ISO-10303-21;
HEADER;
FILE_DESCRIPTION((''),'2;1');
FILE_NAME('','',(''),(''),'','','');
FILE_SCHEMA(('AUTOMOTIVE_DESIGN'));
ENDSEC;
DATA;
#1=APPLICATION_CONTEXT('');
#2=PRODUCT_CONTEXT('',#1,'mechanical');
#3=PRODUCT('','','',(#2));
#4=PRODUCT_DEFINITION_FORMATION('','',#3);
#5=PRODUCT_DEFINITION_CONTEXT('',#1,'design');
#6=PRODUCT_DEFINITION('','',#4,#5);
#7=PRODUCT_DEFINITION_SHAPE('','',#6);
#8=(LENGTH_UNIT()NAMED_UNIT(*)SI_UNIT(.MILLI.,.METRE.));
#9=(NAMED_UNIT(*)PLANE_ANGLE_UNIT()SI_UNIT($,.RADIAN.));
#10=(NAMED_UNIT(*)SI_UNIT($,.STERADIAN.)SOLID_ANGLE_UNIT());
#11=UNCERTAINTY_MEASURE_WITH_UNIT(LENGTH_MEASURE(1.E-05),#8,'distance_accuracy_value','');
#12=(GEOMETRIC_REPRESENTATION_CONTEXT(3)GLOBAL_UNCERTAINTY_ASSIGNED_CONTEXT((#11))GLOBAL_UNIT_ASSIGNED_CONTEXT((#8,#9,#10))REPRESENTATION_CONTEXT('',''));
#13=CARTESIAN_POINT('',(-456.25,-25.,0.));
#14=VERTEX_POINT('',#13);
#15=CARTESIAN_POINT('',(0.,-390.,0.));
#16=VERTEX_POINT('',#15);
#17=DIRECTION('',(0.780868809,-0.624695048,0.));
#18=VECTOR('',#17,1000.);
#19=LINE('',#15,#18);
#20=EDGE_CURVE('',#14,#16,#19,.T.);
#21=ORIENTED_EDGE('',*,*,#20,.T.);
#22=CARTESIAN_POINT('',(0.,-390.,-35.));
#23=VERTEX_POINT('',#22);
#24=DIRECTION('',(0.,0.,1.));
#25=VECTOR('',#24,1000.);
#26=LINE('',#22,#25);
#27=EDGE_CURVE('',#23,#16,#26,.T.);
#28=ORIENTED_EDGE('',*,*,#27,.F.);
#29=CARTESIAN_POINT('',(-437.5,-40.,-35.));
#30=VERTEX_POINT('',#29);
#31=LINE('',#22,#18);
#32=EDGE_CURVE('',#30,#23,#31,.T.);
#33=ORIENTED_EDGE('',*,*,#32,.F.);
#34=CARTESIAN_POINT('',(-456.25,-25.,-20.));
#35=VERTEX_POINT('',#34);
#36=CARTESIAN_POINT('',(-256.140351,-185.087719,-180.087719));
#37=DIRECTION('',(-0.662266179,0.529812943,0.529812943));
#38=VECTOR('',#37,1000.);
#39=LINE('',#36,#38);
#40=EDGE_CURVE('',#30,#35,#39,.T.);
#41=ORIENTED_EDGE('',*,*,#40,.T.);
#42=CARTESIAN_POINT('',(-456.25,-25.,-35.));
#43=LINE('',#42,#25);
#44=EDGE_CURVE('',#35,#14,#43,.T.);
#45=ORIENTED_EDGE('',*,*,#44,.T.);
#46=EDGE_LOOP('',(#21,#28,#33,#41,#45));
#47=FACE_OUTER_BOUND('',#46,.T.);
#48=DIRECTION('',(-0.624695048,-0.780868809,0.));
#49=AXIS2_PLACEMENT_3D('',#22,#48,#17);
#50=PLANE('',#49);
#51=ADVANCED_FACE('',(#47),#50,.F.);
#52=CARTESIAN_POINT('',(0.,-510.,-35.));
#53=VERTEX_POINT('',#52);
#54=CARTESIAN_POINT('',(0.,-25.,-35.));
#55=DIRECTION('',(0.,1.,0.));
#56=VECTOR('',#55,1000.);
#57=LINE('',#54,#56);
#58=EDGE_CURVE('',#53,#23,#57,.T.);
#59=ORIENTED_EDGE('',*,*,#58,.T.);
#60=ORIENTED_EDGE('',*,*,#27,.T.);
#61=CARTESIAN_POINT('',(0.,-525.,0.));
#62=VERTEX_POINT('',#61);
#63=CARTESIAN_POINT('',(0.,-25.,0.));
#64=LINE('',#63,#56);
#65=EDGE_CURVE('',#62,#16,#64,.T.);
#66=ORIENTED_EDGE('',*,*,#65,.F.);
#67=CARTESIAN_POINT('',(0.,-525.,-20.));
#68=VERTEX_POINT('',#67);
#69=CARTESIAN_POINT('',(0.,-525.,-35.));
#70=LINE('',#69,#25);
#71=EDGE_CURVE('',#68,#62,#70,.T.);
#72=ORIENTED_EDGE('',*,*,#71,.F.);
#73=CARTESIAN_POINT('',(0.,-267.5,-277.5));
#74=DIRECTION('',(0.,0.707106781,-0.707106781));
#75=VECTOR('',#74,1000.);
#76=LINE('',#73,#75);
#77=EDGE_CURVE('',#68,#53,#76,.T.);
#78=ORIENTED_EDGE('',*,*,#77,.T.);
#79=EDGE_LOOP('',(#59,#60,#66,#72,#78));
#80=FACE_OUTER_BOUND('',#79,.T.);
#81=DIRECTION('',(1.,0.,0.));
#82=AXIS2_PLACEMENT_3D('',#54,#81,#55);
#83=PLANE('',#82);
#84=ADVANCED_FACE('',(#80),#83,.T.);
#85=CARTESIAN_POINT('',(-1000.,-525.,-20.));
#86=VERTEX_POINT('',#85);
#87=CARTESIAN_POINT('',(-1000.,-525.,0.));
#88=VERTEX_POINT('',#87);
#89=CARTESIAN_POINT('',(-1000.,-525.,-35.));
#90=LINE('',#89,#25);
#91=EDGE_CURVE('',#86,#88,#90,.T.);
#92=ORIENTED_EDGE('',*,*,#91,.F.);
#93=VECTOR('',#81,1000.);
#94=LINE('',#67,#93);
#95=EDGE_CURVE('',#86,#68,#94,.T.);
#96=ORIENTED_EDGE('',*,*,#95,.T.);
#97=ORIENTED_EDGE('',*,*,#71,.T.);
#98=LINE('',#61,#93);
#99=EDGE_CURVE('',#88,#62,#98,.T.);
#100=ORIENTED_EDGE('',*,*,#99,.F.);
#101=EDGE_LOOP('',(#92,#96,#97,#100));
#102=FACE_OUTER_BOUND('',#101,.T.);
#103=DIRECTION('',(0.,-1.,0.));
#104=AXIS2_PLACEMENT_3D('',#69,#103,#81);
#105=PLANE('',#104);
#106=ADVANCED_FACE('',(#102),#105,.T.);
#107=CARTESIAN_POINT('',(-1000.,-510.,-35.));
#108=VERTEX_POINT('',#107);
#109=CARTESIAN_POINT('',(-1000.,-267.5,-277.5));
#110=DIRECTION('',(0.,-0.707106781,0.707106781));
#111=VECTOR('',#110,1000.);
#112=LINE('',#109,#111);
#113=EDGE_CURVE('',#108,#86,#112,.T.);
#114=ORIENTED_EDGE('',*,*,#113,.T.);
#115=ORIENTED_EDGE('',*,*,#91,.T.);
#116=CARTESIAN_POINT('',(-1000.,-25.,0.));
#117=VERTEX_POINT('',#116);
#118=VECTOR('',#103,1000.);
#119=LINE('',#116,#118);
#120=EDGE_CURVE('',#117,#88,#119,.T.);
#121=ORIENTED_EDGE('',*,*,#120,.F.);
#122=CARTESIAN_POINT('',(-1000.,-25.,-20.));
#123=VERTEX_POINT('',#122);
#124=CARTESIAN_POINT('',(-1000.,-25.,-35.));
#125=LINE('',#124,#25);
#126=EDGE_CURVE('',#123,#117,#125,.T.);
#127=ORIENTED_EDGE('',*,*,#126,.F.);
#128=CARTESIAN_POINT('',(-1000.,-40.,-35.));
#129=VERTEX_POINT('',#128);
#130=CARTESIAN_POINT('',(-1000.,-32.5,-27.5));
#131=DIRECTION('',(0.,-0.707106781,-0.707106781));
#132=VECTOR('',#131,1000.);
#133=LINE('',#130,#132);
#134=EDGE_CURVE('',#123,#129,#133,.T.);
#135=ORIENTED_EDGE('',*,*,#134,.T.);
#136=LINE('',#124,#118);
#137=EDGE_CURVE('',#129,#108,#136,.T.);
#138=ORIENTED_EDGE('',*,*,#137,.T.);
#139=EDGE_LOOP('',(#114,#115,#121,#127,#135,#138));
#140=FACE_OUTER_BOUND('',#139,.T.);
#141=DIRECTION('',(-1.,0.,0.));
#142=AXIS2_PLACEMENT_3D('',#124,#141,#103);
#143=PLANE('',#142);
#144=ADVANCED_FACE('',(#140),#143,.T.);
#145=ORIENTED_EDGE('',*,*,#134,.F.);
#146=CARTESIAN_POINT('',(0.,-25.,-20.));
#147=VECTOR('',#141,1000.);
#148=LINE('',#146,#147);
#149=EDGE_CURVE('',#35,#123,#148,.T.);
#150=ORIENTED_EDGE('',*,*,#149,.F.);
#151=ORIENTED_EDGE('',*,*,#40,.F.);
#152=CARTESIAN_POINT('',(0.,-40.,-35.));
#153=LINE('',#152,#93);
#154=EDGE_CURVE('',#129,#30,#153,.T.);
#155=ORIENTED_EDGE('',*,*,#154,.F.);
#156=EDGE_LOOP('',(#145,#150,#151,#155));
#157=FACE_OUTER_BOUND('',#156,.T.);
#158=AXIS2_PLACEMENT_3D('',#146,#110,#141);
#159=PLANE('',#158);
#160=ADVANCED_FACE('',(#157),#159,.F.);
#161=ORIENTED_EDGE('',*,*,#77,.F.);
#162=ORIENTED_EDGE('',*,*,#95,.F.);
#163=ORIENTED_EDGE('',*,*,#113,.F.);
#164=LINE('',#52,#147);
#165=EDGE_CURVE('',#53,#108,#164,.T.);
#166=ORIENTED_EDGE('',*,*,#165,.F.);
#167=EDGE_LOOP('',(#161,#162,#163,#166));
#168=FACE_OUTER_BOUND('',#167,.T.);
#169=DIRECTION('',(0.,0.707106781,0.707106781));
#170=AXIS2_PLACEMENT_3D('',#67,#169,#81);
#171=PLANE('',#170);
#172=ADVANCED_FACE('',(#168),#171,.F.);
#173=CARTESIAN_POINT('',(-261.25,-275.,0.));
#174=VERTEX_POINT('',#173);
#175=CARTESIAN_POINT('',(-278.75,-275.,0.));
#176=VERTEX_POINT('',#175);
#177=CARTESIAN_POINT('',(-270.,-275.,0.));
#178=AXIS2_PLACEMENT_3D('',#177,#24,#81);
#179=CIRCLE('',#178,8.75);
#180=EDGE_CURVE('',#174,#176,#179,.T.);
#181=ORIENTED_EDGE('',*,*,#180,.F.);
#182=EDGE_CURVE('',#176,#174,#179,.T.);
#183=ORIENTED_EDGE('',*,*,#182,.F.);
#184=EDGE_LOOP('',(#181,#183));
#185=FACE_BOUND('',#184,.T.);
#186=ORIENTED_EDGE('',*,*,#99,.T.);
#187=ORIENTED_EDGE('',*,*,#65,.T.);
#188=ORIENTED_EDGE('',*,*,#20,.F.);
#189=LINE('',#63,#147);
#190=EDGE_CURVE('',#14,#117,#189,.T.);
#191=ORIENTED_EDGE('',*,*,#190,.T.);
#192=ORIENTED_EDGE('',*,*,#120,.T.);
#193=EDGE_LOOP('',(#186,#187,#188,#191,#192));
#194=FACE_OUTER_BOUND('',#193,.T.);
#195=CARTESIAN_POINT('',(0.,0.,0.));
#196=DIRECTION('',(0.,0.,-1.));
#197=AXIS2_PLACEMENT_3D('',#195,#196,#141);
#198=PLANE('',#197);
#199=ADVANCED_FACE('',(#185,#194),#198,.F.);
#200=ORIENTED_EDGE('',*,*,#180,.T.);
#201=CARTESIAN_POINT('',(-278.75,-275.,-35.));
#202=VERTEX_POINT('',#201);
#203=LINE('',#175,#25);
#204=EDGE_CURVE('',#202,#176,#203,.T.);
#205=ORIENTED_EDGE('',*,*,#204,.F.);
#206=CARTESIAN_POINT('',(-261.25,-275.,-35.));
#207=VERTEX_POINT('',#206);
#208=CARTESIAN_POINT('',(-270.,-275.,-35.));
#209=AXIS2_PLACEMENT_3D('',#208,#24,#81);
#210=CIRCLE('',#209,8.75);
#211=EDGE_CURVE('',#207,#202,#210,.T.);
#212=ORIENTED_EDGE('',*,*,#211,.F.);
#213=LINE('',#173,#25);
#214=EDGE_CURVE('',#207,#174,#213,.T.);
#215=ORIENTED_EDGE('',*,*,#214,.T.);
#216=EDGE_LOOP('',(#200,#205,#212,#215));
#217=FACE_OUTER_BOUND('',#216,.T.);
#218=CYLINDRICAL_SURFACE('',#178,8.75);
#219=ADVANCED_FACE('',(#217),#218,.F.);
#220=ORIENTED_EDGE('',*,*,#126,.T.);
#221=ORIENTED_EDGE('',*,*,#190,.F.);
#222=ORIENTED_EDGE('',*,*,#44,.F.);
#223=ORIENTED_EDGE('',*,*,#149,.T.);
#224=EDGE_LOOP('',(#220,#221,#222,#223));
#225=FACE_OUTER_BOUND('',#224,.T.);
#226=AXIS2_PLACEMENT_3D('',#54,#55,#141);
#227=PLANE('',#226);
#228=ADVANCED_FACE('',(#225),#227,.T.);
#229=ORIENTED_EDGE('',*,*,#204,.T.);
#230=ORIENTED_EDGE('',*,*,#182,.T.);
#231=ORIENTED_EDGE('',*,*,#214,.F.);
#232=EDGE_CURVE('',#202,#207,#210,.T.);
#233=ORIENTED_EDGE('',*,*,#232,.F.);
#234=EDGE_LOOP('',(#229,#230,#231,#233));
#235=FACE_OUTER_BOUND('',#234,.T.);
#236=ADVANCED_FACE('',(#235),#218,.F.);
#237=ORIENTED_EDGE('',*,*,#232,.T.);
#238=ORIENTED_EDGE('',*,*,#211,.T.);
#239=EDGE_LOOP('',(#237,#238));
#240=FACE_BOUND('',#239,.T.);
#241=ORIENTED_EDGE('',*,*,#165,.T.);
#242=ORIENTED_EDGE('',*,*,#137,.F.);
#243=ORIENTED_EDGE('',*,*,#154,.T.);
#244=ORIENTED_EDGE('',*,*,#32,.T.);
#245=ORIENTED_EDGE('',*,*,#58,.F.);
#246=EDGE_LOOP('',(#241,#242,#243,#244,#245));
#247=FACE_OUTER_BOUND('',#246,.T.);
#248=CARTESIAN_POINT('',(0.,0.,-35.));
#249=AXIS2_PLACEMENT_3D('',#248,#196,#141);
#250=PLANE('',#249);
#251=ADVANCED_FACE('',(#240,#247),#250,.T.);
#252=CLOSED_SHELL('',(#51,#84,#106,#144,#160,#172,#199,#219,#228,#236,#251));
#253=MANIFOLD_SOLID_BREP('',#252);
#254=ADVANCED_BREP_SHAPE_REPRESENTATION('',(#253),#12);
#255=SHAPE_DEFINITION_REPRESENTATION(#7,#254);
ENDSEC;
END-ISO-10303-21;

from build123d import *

# Parameters (mm, degrees)
SKETCH1_W           = 1000
SKETCH1_H           = 500
BOSS_EXTRUDE1_DEPTH = 35
M20_TAPPED_HOLE1_D  = 17.5
CHAMFER1_SIZE       = 15
CUT_EXTRUDE3_DEPTH  = 1130.97787589


with BuildPart() as part:
    # Sketch1 → Boss-Extrude1 (new body)
    with BuildSketch(Plane.XY):
        with Locations((-500, -275)):
            Rectangle(SKETCH1_W, SKETCH1_H)
    extrude(amount=-BOSS_EXTRUDE1_DEPTH)

    # M20 Tapped Hole1 (through all)
    with Locations(Plane(origin=(-30, -275, 0), x_dir=(1, 0, 0), z_dir=(0, 0, 1))):
        with Locations((0, 0), (-240, 0)):
            Hole(M20_TAPPED_HOLE1_D / 2)

    # Chamfer1
    chamfer1_edges = [part.edges().sort_by_distance(p)[0] for p in [
        (-500, -525, -35),
        (-500, -25, -35),
    ]]
    chamfer(chamfer1_edges, length=CHAMFER1_SIZE)

    # Sketch9 → Cut-Extrude3 (cut, through all)
    with BuildSketch(Plane.XY):
        Polygon((-500, 10), (0, 10), (0, -390), align=None)
    extrude(amount=-CUT_EXTRUDE3_DEPTH, mode=Mode.SUBTRACT)


solid = part.part
